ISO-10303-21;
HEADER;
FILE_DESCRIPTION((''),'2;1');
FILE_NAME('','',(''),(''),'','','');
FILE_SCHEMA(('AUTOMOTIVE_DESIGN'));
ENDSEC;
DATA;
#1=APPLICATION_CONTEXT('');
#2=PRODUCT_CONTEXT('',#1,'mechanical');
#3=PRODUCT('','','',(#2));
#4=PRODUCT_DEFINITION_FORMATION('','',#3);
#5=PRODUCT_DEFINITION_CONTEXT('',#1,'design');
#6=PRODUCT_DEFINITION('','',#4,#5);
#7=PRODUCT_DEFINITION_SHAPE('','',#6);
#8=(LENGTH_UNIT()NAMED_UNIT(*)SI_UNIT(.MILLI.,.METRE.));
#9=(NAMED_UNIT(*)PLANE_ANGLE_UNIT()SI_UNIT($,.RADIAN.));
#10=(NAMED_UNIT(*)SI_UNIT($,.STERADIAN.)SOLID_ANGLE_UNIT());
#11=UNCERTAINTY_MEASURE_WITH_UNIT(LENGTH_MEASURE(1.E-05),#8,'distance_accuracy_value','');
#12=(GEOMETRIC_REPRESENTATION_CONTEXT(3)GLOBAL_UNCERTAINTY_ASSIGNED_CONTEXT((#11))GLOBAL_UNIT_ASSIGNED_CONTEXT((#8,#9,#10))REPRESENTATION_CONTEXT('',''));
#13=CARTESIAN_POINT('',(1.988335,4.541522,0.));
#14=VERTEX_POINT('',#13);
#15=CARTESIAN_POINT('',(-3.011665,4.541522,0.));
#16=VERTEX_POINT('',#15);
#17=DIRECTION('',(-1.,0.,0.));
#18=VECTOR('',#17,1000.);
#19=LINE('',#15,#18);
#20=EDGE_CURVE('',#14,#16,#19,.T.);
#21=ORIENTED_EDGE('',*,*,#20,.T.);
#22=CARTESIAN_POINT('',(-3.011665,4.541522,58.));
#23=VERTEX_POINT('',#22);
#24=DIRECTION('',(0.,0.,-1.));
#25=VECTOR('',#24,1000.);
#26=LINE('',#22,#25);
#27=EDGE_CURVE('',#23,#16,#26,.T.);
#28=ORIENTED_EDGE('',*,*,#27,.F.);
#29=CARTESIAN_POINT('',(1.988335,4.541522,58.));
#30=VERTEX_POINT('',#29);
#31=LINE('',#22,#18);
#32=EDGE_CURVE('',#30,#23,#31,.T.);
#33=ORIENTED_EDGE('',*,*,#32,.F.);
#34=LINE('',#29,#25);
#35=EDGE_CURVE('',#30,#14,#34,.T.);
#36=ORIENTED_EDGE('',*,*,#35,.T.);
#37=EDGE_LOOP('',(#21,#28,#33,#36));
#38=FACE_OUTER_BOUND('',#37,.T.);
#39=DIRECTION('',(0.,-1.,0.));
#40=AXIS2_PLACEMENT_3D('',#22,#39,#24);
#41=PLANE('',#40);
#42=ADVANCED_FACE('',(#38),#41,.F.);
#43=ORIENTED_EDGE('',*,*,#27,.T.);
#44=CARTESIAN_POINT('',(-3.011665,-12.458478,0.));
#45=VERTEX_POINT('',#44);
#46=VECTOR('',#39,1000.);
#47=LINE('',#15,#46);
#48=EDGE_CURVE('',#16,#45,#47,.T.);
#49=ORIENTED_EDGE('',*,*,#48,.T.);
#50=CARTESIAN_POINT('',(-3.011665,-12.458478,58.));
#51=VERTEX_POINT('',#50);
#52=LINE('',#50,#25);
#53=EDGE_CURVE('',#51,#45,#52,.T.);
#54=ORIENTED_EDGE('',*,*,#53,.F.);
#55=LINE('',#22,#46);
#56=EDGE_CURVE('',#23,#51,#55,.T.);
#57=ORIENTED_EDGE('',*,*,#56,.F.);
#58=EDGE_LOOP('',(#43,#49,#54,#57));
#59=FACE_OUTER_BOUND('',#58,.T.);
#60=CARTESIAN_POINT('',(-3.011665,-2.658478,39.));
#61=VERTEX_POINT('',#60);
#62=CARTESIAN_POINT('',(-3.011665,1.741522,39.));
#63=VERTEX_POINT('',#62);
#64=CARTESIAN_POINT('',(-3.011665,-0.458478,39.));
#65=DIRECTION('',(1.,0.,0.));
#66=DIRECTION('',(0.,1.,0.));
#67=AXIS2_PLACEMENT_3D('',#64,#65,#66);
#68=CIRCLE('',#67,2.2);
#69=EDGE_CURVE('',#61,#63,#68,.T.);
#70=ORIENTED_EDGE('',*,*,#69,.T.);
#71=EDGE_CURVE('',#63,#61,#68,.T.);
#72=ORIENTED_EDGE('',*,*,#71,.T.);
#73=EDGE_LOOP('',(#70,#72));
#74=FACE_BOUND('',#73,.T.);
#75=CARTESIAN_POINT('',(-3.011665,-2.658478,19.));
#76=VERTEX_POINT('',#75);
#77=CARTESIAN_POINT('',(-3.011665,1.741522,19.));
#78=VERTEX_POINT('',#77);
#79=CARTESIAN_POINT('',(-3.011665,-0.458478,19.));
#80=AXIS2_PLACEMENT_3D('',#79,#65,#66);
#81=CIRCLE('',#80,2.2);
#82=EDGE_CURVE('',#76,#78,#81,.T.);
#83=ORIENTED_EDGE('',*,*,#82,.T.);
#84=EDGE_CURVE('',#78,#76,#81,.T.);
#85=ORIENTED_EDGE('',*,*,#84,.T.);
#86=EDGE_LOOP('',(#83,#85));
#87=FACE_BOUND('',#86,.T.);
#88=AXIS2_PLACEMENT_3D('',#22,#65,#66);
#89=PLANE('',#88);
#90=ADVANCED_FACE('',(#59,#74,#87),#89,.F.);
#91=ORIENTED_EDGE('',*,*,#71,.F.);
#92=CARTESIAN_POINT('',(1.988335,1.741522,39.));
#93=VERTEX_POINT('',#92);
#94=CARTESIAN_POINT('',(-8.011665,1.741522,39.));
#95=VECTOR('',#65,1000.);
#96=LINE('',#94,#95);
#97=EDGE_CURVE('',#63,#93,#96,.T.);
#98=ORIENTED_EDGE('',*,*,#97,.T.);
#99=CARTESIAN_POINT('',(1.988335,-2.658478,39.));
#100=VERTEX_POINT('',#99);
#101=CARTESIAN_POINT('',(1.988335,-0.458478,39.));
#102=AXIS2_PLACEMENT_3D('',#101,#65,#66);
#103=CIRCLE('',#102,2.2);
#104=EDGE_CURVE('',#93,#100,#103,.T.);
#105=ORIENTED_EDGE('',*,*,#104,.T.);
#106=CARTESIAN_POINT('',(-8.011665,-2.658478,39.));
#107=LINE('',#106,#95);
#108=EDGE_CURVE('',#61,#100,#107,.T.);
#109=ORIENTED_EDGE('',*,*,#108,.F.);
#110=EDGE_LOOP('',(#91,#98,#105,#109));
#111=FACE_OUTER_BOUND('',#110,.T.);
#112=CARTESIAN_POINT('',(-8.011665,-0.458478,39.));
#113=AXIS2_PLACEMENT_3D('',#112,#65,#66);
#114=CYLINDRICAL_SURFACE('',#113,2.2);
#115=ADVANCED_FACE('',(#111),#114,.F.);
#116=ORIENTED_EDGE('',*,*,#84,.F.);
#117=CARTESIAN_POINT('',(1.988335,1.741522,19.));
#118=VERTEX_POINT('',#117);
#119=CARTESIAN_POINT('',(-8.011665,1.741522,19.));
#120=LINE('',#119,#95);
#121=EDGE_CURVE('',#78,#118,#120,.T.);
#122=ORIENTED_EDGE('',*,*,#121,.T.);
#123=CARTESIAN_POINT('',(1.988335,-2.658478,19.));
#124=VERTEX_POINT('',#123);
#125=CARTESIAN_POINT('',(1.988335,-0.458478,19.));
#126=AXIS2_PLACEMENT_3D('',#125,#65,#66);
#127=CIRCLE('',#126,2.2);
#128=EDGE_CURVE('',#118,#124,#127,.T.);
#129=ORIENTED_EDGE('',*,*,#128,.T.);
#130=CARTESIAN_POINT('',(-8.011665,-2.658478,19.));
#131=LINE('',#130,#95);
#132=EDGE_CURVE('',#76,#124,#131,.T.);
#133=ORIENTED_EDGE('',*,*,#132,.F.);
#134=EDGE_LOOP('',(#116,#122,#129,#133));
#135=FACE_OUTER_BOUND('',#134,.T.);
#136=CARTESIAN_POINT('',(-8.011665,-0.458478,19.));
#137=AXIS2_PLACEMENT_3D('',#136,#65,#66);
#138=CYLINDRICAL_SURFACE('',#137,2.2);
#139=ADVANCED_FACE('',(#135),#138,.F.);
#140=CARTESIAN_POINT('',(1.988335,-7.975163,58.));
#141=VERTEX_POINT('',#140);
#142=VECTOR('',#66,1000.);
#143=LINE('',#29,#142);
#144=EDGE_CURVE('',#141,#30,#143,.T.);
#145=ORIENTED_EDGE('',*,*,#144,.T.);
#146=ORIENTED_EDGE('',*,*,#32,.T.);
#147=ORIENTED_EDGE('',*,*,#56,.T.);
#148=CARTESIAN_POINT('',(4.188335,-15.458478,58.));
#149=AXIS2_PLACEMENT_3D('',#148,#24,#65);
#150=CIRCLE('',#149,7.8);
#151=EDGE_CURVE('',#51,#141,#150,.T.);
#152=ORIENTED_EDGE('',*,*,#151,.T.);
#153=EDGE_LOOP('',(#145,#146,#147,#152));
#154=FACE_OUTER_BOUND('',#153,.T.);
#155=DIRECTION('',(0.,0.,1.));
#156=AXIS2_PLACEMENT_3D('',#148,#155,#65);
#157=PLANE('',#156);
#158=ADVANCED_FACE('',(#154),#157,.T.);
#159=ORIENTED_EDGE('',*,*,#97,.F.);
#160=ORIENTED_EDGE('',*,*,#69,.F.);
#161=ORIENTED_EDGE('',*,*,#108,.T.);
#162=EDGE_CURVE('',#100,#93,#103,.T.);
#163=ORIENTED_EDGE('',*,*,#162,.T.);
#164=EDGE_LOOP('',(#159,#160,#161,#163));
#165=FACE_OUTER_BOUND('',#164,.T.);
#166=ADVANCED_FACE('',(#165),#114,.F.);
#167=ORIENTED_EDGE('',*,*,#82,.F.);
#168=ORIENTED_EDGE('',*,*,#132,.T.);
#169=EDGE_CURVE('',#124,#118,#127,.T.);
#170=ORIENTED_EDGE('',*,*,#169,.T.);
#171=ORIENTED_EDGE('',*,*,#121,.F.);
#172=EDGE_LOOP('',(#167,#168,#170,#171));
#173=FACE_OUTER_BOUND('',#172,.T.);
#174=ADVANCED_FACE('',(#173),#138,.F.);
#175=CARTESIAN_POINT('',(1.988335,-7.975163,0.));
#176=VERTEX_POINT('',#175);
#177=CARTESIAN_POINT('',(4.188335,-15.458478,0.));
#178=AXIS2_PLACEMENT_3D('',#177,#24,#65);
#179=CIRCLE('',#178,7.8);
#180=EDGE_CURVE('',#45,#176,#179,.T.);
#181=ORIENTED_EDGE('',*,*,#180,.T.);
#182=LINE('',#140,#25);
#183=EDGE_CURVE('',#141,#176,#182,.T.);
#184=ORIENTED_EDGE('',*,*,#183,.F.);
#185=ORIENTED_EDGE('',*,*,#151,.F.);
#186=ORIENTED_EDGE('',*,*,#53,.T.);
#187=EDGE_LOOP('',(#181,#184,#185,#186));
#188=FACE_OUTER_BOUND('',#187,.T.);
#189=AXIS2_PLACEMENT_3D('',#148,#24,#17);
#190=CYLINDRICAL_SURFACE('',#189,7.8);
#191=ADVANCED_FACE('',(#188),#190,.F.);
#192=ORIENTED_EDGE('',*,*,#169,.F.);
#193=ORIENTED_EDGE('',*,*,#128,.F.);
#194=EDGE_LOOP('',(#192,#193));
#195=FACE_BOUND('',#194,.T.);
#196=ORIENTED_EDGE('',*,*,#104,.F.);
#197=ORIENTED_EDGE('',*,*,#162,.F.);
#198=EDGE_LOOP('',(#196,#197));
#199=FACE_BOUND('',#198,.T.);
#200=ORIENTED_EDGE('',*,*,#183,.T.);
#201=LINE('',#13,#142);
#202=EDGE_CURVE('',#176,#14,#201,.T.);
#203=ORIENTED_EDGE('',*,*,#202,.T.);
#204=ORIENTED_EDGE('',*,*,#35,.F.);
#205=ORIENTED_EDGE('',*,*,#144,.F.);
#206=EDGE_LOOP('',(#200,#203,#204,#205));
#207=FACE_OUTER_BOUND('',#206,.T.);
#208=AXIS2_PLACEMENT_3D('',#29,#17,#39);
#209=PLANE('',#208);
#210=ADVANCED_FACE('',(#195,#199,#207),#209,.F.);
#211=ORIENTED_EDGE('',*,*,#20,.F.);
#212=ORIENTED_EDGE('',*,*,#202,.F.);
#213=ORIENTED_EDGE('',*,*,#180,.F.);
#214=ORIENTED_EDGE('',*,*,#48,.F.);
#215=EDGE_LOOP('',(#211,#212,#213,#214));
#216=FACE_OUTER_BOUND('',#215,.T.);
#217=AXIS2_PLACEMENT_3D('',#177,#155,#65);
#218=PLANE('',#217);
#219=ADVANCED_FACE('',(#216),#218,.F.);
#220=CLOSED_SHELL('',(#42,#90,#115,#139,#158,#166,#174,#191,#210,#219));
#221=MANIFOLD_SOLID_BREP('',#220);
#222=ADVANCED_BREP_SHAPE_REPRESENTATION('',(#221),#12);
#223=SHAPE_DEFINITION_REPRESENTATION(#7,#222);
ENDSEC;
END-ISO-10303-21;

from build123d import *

# Parameters (mm, degrees)
EXTRUDE_1_DEPTH     = 58
SKETCH_2_R          = 2.2
CUT_EXTRUDE_1_DEPTH = 10


with BuildPart() as part:
    # 草图1 → 凸台-拉伸1 (new body)
    with BuildSketch(Plane.XY):
        with BuildLine():
            Line((-3.011664558, 4.541522048), (1.988335442, 4.541522048))
            Line((1.988335442, 4.541522048), (1.988335442, -7.975163179))
            ThreePointArc((1.988335442, -7.975163179), (-1.018873776, -9.651157386), (-3.011664558, -12.458477952))
            Line((-3.011664558, -12.458477952), (-3.011664558, 4.541522048))
        make_face()
    extrude(amount=EXTRUDE_1_DEPTH)

    # 草图2 → 切除-拉伸1 (cut)
    with BuildSketch(Plane(origin=(1.988335442, 0, 0), x_dir=(0, 0, -1), z_dir=(1, 0, 0))):
        with Locations(Location((-19, -0.458477952, 0), (0, 0, 90))):
            Circle(SKETCH_2_R)
        with Locations(Location((-39, -0.458477952, 0), (0, 0, 90))):
            Circle(SKETCH_2_R)
    extrude(amount=-CUT_EXTRUDE_1_DEPTH, mode=Mode.SUBTRACT)


solid = part.part
